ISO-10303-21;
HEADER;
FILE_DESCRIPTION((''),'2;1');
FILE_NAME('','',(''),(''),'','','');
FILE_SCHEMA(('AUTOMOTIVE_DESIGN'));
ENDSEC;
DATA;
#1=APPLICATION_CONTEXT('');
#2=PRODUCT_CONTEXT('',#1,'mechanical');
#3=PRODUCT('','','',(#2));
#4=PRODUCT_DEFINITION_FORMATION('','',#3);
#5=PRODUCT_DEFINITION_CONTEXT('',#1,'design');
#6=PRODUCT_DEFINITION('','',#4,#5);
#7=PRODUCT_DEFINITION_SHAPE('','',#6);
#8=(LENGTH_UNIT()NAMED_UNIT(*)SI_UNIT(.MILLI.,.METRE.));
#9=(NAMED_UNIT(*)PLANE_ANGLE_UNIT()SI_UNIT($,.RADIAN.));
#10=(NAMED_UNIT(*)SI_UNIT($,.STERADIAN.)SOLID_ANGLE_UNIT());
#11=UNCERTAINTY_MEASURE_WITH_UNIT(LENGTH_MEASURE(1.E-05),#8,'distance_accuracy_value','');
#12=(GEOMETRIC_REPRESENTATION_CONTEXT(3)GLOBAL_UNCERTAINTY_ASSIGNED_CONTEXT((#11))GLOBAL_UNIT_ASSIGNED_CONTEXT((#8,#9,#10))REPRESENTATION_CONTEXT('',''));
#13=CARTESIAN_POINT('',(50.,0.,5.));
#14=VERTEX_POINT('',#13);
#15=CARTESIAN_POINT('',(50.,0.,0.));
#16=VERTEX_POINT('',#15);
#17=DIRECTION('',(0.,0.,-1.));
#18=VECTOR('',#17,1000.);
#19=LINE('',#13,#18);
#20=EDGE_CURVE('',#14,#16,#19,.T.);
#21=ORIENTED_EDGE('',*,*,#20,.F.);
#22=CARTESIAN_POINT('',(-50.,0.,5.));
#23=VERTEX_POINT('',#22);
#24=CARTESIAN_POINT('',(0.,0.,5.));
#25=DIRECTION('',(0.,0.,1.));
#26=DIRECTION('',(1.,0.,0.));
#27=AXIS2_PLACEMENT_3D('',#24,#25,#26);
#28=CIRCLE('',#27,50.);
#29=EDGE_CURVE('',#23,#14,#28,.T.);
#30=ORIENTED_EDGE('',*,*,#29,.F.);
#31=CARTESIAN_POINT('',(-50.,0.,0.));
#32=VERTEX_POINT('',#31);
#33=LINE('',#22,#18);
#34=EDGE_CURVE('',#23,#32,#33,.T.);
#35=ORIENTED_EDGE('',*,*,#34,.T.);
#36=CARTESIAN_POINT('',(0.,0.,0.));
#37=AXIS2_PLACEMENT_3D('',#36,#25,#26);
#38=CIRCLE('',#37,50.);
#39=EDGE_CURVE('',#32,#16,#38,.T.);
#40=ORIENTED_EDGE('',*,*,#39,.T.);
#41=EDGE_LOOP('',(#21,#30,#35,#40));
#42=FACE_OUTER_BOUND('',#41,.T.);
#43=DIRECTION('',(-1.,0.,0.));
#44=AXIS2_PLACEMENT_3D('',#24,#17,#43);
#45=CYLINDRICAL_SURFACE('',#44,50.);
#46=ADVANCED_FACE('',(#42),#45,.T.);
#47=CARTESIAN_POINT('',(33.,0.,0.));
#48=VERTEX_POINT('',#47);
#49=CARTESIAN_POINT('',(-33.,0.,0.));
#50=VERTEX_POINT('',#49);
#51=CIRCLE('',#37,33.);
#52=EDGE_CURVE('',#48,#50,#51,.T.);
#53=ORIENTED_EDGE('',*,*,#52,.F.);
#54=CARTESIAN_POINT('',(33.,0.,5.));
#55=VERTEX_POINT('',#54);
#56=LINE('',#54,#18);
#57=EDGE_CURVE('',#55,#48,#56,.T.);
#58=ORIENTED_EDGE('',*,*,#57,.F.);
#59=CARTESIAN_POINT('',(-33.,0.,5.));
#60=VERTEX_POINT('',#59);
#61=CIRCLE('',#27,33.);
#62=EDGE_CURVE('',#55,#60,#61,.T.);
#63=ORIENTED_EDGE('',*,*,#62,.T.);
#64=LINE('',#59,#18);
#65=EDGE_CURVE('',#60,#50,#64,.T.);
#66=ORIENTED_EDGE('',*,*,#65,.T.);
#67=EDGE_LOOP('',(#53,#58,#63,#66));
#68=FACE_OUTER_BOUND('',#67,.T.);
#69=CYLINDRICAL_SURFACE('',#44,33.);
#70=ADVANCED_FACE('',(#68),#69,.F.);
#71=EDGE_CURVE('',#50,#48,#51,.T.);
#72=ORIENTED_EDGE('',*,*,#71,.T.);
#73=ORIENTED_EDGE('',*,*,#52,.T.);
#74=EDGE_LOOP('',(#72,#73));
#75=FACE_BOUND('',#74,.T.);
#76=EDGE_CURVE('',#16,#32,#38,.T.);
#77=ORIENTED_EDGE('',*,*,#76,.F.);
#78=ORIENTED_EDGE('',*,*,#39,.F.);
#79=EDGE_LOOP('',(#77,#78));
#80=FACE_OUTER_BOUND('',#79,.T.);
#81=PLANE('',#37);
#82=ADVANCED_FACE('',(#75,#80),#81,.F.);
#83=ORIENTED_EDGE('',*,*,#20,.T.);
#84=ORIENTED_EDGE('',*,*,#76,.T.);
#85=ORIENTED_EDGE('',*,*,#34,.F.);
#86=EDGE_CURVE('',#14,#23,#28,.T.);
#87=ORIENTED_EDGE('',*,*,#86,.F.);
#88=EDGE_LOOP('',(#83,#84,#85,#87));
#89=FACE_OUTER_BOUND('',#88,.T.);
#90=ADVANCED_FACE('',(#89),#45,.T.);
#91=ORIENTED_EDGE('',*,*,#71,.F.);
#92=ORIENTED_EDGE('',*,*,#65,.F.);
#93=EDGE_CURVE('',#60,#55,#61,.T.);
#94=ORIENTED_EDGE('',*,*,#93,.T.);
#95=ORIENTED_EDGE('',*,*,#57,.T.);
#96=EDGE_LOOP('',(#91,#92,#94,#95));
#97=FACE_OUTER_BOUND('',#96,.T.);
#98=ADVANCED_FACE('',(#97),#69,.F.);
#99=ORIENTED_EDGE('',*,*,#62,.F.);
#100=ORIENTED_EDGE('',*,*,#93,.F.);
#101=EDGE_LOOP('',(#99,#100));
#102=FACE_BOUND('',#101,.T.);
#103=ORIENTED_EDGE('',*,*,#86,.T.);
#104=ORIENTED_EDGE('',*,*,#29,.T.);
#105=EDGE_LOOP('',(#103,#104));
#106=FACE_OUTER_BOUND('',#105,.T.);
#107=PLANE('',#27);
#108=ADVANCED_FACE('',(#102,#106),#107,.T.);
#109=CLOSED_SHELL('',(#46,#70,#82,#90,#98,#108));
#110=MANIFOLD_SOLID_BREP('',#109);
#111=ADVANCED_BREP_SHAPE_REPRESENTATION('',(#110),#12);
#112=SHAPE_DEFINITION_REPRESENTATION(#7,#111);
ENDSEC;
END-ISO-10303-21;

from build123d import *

# Parameters (mm, degrees)
SKETCH_1_R      = 50
SKETCH_1_R_2    = 33
EXTRUDE_1_DEPTH = 5


with BuildPart() as part:
    # 草图1 → 凸台-拉伸1 (new body)
    with BuildSketch(Plane.XY):
        Circle(SKETCH_1_R)
        Circle(SKETCH_1_R_2, mode=Mode.SUBTRACT)
    extrude(amount=EXTRUDE_1_DEPTH)


solid = part.part
